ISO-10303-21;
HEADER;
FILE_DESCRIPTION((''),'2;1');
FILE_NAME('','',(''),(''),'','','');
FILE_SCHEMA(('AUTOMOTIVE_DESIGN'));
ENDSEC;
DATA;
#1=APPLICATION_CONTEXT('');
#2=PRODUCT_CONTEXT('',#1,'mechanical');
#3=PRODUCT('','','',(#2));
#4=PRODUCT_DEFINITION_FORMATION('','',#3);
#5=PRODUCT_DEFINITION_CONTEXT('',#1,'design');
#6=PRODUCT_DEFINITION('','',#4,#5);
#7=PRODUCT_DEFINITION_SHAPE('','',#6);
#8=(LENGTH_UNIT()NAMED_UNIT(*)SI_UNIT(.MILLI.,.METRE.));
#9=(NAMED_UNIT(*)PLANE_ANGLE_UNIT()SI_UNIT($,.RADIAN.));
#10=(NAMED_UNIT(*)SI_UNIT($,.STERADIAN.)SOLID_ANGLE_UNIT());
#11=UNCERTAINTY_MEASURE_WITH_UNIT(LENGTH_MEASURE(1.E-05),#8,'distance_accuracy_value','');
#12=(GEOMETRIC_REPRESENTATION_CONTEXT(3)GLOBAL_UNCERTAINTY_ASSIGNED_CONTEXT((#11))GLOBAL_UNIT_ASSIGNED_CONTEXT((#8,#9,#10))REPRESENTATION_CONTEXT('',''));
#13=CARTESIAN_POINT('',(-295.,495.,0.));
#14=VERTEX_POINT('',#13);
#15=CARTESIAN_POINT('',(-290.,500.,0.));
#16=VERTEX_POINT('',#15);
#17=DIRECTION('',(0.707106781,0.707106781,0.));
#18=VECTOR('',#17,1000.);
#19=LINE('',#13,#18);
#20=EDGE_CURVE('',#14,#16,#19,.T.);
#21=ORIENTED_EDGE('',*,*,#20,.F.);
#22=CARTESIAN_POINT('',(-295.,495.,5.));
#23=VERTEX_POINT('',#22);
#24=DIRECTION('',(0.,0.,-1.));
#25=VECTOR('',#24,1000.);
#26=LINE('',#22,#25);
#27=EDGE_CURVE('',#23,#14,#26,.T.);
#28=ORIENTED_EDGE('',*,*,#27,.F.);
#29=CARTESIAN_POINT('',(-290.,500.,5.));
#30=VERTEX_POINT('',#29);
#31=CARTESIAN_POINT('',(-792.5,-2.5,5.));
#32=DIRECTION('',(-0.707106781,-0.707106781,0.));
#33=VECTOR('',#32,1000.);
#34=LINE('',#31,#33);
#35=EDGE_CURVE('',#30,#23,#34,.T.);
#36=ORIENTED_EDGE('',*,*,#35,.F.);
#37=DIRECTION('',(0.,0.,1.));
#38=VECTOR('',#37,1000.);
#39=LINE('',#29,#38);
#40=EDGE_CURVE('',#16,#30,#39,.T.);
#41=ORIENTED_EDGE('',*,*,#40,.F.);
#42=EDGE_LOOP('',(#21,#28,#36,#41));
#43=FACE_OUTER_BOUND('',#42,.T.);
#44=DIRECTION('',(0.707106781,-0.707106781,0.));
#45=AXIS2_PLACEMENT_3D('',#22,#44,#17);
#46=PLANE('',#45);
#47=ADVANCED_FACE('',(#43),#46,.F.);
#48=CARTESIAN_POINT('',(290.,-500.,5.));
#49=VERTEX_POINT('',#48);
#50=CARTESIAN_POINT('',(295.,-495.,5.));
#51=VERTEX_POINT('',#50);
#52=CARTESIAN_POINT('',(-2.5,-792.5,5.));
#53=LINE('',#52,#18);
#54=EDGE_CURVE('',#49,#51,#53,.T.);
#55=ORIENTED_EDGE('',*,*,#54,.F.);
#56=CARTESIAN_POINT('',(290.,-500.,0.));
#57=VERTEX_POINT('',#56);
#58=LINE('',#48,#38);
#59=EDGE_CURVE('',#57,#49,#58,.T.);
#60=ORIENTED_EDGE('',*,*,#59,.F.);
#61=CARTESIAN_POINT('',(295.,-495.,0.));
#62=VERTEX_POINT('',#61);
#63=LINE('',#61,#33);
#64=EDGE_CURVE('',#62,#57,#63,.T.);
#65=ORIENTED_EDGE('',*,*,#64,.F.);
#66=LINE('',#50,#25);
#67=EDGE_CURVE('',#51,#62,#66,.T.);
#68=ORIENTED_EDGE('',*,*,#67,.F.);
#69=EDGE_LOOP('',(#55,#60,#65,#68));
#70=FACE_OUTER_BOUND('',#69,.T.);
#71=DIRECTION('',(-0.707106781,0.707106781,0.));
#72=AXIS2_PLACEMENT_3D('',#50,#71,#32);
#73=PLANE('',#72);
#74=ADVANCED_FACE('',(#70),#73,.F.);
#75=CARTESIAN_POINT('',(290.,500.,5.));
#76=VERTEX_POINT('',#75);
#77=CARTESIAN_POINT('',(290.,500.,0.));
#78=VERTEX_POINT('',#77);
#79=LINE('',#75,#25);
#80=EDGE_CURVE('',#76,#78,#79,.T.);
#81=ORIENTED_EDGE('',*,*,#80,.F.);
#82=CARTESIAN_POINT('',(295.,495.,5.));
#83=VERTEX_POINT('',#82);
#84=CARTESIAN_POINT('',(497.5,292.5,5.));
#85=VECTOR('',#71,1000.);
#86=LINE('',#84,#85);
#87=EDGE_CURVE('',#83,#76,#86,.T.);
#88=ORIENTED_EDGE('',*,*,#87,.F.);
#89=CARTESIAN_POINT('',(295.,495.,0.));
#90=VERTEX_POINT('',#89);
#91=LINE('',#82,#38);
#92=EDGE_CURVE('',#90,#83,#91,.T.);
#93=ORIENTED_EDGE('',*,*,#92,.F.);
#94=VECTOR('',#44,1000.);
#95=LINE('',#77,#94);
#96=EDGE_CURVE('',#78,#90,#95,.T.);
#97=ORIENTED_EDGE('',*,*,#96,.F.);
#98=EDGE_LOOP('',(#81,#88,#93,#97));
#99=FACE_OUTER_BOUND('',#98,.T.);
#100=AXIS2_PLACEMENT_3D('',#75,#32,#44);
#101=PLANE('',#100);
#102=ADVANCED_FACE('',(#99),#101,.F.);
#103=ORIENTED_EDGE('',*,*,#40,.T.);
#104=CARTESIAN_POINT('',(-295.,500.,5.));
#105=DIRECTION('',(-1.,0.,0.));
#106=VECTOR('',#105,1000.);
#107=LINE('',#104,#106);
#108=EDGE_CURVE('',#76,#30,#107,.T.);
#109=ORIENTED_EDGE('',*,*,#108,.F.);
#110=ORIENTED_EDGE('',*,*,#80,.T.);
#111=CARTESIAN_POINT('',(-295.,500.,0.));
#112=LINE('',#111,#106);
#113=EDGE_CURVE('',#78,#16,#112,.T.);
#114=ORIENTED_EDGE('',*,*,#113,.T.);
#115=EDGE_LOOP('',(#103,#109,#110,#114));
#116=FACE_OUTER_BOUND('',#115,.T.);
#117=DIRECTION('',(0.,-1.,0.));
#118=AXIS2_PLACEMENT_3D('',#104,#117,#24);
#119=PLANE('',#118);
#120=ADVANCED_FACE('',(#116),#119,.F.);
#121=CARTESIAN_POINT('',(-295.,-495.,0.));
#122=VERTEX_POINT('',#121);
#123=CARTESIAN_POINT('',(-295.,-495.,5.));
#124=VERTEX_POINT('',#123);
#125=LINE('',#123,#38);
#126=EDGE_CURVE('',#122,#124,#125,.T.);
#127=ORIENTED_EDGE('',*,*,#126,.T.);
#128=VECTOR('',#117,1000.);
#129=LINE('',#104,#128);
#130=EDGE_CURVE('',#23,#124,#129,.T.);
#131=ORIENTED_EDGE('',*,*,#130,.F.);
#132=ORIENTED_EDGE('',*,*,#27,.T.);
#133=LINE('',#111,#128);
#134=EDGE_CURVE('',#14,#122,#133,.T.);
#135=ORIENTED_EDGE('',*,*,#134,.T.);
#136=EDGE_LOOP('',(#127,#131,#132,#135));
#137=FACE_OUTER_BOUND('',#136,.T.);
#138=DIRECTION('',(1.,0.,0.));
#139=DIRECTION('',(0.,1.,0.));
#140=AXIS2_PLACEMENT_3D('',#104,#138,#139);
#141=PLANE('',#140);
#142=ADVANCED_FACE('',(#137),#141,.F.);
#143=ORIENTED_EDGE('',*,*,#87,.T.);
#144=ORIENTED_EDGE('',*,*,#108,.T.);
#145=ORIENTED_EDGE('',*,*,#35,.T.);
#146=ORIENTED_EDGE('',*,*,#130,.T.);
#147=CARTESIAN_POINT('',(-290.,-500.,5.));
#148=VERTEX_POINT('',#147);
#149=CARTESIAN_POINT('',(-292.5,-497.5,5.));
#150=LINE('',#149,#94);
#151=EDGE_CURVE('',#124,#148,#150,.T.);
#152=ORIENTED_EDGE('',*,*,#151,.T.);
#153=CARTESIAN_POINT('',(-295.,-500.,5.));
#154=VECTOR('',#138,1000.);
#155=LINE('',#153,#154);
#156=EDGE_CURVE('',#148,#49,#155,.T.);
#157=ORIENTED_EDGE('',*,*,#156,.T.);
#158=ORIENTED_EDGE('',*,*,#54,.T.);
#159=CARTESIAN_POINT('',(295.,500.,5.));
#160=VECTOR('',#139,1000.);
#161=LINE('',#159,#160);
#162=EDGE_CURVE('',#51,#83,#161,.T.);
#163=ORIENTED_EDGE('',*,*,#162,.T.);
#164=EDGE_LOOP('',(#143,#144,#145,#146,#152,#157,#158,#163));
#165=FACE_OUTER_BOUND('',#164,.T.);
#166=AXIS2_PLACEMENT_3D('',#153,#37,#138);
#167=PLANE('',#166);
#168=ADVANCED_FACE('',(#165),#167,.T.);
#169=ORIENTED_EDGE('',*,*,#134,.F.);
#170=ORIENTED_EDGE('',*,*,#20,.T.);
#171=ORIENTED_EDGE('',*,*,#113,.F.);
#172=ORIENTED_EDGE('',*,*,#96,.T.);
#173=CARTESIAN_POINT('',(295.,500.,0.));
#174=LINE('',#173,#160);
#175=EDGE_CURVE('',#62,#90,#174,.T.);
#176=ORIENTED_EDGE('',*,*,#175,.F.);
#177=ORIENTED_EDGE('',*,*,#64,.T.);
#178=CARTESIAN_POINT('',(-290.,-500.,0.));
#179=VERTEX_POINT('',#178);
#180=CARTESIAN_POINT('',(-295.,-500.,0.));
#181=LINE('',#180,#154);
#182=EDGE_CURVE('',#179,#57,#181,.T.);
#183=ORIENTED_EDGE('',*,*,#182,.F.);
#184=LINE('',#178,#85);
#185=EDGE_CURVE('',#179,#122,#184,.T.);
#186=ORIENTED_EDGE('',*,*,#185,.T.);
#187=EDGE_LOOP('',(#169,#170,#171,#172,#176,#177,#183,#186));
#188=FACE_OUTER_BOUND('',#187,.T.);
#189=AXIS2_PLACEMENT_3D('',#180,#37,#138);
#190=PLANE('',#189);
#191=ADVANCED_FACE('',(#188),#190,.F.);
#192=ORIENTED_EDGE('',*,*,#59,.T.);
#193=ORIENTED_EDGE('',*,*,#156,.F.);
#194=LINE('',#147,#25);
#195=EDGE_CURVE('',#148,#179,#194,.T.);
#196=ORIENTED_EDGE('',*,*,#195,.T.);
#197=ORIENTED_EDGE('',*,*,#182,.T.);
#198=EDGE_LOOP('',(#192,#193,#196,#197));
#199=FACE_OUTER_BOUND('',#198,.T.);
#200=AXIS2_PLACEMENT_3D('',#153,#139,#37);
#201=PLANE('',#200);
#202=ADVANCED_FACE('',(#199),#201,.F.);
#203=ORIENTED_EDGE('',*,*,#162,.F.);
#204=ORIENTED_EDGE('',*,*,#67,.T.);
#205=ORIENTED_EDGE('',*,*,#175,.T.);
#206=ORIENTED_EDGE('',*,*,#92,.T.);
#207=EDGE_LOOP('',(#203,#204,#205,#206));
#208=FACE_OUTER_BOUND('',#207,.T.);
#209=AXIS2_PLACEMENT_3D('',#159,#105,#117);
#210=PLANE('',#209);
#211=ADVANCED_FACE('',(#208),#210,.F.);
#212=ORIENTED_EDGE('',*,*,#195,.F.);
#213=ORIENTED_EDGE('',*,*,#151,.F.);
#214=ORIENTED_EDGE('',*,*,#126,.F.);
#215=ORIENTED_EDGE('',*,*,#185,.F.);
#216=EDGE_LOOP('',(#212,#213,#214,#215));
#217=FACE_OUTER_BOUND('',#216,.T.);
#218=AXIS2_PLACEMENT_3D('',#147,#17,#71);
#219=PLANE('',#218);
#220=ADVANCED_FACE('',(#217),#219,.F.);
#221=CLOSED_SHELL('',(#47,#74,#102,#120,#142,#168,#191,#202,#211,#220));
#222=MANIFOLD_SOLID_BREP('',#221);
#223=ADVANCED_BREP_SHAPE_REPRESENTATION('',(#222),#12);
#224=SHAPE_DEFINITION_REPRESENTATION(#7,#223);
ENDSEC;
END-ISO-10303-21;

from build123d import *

# Parameters (mm, degrees)
SKETCH_1_W      = 590
SKETCH_1_H      = 1000
EXTRUDE_1_DEPTH = 5
CHAMFER_1_SIZE  = 5


with BuildPart() as part:
    # 草图1 → 拉伸1 (new body)
    with BuildSketch(Plane.XY):
        Rectangle(SKETCH_1_W, SKETCH_1_H)
    extrude(amount=EXTRUDE_1_DEPTH)

    # 倒角1
    chamfer_1_edges = [part.edges().sort_by_distance(p)[0] for p in [
        (-295, 500, 2.5),
        (295, 500, 2.5),
        (295, -500, 2.5),
        (-295, -500, 2.5),
    ]]
    chamfer(chamfer_1_edges, length=CHAMFER_1_SIZE)


solid = part.part
